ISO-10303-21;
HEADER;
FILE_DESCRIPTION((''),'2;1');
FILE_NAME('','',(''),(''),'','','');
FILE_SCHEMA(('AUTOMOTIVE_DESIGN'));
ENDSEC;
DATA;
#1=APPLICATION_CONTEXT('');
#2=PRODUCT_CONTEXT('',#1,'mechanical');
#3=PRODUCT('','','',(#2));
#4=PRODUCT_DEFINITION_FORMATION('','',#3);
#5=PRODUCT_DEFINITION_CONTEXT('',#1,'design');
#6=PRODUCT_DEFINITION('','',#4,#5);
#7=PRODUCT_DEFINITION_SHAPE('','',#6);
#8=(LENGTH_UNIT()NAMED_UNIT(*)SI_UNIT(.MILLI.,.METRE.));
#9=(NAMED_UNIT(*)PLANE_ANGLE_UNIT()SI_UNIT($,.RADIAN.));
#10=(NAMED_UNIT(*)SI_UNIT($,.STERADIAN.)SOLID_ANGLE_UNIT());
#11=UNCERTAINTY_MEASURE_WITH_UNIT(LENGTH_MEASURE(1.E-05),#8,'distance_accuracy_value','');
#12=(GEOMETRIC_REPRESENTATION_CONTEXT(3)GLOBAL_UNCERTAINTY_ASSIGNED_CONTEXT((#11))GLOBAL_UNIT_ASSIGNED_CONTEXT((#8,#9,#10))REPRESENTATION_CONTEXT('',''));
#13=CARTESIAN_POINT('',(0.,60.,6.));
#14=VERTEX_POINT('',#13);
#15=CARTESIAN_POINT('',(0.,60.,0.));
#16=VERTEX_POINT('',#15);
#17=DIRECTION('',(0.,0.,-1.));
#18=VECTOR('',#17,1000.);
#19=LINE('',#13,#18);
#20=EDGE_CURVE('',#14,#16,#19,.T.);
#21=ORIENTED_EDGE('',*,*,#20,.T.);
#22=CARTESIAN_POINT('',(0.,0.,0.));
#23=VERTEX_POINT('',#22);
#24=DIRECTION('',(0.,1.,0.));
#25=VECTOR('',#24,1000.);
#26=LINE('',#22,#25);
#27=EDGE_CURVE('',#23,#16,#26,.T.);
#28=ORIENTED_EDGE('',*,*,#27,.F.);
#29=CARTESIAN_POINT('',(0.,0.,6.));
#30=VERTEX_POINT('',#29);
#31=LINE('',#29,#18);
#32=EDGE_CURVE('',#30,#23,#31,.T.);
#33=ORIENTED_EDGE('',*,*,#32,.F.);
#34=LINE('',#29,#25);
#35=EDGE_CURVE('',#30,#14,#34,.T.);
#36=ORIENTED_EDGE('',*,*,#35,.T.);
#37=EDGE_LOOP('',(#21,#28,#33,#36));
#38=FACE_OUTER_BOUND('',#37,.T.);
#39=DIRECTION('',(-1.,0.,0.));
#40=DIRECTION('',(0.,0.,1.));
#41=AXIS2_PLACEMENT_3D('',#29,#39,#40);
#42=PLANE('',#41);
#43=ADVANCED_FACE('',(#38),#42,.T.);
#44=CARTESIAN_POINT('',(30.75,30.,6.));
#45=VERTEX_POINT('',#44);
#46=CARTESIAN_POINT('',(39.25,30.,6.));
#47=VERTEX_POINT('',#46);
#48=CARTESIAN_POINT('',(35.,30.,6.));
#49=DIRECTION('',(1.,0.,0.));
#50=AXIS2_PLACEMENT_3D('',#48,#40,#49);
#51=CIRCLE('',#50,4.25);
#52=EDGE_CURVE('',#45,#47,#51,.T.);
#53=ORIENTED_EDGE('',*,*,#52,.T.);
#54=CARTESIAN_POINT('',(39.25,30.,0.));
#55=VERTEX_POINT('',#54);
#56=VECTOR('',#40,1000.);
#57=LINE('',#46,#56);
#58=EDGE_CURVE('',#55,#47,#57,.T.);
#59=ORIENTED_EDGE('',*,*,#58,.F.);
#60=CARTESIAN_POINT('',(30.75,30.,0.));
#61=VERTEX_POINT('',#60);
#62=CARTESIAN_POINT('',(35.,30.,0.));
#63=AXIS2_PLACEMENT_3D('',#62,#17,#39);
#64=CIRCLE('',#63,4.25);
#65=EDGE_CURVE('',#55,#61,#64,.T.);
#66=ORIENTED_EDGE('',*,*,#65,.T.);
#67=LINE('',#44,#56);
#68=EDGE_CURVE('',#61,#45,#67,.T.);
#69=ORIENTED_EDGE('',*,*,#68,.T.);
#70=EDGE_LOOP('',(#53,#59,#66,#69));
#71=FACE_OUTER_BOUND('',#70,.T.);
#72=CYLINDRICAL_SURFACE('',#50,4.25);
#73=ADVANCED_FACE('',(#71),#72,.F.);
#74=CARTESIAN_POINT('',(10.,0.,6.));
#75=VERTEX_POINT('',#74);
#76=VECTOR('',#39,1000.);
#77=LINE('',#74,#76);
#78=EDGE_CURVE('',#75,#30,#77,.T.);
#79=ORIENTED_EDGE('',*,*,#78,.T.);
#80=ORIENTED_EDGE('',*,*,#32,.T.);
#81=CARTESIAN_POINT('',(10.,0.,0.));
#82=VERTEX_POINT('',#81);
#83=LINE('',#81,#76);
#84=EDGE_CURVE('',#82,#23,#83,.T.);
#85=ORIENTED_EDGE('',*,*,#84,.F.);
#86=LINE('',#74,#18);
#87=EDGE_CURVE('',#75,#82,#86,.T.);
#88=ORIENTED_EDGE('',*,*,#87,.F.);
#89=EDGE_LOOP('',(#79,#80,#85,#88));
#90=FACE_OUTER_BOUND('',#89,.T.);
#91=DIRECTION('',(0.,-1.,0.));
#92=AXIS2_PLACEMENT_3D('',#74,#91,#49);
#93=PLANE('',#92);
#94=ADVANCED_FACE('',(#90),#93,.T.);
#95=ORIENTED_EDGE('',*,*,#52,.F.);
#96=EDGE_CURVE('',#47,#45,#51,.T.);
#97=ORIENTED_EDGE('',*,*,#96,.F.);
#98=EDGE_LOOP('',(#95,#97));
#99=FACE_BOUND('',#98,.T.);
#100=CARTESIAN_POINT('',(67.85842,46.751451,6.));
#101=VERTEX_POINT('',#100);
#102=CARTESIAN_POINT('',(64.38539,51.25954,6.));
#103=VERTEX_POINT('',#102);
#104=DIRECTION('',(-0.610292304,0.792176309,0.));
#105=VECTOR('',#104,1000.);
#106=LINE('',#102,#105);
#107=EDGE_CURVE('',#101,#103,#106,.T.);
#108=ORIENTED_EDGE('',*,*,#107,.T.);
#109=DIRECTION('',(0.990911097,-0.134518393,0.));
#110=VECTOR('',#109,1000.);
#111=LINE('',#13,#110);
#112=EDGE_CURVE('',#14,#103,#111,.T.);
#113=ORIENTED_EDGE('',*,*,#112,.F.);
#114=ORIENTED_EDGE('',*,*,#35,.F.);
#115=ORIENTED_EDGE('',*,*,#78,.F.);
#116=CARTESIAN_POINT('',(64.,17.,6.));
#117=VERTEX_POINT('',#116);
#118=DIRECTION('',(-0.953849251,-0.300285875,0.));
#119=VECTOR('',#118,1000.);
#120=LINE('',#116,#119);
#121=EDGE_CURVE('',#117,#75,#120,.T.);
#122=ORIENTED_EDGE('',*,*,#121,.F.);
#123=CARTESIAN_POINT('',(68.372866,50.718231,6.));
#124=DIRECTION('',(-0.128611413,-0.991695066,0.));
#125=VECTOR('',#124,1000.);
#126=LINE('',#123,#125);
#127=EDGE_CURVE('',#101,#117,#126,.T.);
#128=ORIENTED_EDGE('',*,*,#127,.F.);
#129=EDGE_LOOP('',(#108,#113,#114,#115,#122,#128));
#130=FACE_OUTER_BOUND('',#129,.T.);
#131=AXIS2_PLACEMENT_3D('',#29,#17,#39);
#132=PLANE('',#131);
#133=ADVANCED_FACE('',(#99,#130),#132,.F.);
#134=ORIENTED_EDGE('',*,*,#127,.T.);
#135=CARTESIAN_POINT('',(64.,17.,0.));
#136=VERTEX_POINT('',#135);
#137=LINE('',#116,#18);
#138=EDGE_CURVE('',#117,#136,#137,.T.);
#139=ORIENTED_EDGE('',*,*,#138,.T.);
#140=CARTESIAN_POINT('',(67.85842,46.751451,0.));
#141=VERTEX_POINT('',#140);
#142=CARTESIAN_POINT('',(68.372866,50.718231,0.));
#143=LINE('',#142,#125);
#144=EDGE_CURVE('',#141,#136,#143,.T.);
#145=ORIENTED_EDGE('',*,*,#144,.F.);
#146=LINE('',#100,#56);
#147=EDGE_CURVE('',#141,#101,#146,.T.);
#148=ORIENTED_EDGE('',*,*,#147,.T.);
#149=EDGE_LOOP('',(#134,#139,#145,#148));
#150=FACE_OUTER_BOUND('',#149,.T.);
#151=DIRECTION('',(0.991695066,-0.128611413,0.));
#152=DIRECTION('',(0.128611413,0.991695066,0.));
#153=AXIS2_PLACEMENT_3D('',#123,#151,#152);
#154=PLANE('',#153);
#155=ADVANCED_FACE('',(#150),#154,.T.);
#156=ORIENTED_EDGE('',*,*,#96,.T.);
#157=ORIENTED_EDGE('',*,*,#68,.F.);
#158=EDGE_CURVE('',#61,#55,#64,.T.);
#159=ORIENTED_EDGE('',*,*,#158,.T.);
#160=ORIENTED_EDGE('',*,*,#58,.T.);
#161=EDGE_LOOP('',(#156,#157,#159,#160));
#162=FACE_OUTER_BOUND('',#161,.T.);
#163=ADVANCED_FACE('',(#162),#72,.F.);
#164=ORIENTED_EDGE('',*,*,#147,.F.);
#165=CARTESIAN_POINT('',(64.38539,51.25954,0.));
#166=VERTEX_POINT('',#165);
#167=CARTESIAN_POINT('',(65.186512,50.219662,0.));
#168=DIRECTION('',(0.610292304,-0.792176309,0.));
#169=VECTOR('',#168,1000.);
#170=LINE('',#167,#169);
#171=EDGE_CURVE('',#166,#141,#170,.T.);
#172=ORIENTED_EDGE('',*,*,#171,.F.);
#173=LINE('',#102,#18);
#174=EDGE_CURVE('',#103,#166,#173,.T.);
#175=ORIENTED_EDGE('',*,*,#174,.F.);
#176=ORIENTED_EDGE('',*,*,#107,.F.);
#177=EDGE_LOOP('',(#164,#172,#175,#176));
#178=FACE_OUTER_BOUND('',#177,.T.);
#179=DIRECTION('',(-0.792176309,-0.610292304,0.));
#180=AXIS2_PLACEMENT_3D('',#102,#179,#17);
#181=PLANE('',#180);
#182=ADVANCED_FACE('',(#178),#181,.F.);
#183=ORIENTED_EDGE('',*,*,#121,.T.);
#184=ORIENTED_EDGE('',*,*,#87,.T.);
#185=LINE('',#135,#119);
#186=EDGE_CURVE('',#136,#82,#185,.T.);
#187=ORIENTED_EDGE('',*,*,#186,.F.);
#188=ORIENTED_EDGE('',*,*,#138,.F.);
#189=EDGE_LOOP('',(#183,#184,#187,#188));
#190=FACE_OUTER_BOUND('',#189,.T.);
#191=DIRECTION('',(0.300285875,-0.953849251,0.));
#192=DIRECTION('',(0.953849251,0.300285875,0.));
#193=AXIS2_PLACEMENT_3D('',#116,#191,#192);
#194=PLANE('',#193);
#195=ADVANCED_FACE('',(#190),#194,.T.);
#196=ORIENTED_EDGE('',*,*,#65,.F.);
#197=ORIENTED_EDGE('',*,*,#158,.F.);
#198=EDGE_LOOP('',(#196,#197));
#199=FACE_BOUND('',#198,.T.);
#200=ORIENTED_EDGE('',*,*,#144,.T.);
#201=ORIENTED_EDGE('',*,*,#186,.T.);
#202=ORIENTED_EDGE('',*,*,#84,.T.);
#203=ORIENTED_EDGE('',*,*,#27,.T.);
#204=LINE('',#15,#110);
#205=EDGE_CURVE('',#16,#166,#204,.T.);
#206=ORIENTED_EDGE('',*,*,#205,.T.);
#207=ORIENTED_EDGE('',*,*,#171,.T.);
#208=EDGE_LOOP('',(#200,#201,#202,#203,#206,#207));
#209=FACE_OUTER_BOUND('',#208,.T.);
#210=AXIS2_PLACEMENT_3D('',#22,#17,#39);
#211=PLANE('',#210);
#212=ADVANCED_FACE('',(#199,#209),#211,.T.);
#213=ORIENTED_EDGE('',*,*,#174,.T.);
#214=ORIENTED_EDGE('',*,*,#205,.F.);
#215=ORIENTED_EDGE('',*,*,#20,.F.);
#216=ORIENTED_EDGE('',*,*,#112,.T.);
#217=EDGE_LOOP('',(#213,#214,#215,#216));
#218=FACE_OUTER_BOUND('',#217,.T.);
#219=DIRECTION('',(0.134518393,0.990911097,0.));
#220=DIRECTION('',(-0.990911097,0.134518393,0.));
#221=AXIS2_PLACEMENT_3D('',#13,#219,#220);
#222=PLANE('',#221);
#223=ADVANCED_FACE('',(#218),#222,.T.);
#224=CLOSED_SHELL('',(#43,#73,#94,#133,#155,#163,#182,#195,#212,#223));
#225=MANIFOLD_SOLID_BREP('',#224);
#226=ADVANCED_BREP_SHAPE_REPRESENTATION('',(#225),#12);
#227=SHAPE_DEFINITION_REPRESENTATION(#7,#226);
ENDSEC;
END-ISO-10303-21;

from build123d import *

# Parameters (mm, degrees)
BOSS_EXTRUDE1_DEPTH    = 6
M10_TAPPED_HOLE2_D     = 8.5
M10_TAPPED_HOLE2_DEPTH = 24.5
M10_TAPPED_HOLE2_TIP   = 2.553657631
CHAMFER1_SIZE          = 4
CHAMFER1_SIZE2         = 4.024049749


with BuildPart() as part:
    # Sketch1 → Boss-Extrude1 (new body)
    with BuildSketch(Plane.XY):
        Polygon((0, 0), (0, 60), (68.372865684, 50.718230869), (64, 17), (10, 0), align=None)
    extrude(amount=BOSS_EXTRUDE1_DEPTH)

    # M10 Tapped Hole2
    with Locations(Plane.XY.offset(6)):
        with Locations((35, 30)):
            Hole(M10_TAPPED_HOLE2_D / 2, depth=M10_TAPPED_HOLE2_DEPTH)
            with Locations((0, 0, -(M10_TAPPED_HOLE2_DEPTH + M10_TAPPED_HOLE2_TIP / 2))):  # 118° drill point
                Cone(0, M10_TAPPED_HOLE2_D / 2, M10_TAPPED_HOLE2_TIP, mode=Mode.SUBTRACT)

    # Chamfer1
    chamfer1_edges = [part.edges().sort_by_distance(p)[0] for p in [
        (68.372865684, 50.718230869, 3),
    ]]
    chamfer1_side = [part.faces().sort_by_distance(p)[0] for p in [
        (66.186432842, 33.859115434, 3),
    ]]
    chamfer(chamfer1_edges, length=CHAMFER1_SIZE, length2=CHAMFER1_SIZE2, reference=chamfer1_side[0])


solid = part.part
